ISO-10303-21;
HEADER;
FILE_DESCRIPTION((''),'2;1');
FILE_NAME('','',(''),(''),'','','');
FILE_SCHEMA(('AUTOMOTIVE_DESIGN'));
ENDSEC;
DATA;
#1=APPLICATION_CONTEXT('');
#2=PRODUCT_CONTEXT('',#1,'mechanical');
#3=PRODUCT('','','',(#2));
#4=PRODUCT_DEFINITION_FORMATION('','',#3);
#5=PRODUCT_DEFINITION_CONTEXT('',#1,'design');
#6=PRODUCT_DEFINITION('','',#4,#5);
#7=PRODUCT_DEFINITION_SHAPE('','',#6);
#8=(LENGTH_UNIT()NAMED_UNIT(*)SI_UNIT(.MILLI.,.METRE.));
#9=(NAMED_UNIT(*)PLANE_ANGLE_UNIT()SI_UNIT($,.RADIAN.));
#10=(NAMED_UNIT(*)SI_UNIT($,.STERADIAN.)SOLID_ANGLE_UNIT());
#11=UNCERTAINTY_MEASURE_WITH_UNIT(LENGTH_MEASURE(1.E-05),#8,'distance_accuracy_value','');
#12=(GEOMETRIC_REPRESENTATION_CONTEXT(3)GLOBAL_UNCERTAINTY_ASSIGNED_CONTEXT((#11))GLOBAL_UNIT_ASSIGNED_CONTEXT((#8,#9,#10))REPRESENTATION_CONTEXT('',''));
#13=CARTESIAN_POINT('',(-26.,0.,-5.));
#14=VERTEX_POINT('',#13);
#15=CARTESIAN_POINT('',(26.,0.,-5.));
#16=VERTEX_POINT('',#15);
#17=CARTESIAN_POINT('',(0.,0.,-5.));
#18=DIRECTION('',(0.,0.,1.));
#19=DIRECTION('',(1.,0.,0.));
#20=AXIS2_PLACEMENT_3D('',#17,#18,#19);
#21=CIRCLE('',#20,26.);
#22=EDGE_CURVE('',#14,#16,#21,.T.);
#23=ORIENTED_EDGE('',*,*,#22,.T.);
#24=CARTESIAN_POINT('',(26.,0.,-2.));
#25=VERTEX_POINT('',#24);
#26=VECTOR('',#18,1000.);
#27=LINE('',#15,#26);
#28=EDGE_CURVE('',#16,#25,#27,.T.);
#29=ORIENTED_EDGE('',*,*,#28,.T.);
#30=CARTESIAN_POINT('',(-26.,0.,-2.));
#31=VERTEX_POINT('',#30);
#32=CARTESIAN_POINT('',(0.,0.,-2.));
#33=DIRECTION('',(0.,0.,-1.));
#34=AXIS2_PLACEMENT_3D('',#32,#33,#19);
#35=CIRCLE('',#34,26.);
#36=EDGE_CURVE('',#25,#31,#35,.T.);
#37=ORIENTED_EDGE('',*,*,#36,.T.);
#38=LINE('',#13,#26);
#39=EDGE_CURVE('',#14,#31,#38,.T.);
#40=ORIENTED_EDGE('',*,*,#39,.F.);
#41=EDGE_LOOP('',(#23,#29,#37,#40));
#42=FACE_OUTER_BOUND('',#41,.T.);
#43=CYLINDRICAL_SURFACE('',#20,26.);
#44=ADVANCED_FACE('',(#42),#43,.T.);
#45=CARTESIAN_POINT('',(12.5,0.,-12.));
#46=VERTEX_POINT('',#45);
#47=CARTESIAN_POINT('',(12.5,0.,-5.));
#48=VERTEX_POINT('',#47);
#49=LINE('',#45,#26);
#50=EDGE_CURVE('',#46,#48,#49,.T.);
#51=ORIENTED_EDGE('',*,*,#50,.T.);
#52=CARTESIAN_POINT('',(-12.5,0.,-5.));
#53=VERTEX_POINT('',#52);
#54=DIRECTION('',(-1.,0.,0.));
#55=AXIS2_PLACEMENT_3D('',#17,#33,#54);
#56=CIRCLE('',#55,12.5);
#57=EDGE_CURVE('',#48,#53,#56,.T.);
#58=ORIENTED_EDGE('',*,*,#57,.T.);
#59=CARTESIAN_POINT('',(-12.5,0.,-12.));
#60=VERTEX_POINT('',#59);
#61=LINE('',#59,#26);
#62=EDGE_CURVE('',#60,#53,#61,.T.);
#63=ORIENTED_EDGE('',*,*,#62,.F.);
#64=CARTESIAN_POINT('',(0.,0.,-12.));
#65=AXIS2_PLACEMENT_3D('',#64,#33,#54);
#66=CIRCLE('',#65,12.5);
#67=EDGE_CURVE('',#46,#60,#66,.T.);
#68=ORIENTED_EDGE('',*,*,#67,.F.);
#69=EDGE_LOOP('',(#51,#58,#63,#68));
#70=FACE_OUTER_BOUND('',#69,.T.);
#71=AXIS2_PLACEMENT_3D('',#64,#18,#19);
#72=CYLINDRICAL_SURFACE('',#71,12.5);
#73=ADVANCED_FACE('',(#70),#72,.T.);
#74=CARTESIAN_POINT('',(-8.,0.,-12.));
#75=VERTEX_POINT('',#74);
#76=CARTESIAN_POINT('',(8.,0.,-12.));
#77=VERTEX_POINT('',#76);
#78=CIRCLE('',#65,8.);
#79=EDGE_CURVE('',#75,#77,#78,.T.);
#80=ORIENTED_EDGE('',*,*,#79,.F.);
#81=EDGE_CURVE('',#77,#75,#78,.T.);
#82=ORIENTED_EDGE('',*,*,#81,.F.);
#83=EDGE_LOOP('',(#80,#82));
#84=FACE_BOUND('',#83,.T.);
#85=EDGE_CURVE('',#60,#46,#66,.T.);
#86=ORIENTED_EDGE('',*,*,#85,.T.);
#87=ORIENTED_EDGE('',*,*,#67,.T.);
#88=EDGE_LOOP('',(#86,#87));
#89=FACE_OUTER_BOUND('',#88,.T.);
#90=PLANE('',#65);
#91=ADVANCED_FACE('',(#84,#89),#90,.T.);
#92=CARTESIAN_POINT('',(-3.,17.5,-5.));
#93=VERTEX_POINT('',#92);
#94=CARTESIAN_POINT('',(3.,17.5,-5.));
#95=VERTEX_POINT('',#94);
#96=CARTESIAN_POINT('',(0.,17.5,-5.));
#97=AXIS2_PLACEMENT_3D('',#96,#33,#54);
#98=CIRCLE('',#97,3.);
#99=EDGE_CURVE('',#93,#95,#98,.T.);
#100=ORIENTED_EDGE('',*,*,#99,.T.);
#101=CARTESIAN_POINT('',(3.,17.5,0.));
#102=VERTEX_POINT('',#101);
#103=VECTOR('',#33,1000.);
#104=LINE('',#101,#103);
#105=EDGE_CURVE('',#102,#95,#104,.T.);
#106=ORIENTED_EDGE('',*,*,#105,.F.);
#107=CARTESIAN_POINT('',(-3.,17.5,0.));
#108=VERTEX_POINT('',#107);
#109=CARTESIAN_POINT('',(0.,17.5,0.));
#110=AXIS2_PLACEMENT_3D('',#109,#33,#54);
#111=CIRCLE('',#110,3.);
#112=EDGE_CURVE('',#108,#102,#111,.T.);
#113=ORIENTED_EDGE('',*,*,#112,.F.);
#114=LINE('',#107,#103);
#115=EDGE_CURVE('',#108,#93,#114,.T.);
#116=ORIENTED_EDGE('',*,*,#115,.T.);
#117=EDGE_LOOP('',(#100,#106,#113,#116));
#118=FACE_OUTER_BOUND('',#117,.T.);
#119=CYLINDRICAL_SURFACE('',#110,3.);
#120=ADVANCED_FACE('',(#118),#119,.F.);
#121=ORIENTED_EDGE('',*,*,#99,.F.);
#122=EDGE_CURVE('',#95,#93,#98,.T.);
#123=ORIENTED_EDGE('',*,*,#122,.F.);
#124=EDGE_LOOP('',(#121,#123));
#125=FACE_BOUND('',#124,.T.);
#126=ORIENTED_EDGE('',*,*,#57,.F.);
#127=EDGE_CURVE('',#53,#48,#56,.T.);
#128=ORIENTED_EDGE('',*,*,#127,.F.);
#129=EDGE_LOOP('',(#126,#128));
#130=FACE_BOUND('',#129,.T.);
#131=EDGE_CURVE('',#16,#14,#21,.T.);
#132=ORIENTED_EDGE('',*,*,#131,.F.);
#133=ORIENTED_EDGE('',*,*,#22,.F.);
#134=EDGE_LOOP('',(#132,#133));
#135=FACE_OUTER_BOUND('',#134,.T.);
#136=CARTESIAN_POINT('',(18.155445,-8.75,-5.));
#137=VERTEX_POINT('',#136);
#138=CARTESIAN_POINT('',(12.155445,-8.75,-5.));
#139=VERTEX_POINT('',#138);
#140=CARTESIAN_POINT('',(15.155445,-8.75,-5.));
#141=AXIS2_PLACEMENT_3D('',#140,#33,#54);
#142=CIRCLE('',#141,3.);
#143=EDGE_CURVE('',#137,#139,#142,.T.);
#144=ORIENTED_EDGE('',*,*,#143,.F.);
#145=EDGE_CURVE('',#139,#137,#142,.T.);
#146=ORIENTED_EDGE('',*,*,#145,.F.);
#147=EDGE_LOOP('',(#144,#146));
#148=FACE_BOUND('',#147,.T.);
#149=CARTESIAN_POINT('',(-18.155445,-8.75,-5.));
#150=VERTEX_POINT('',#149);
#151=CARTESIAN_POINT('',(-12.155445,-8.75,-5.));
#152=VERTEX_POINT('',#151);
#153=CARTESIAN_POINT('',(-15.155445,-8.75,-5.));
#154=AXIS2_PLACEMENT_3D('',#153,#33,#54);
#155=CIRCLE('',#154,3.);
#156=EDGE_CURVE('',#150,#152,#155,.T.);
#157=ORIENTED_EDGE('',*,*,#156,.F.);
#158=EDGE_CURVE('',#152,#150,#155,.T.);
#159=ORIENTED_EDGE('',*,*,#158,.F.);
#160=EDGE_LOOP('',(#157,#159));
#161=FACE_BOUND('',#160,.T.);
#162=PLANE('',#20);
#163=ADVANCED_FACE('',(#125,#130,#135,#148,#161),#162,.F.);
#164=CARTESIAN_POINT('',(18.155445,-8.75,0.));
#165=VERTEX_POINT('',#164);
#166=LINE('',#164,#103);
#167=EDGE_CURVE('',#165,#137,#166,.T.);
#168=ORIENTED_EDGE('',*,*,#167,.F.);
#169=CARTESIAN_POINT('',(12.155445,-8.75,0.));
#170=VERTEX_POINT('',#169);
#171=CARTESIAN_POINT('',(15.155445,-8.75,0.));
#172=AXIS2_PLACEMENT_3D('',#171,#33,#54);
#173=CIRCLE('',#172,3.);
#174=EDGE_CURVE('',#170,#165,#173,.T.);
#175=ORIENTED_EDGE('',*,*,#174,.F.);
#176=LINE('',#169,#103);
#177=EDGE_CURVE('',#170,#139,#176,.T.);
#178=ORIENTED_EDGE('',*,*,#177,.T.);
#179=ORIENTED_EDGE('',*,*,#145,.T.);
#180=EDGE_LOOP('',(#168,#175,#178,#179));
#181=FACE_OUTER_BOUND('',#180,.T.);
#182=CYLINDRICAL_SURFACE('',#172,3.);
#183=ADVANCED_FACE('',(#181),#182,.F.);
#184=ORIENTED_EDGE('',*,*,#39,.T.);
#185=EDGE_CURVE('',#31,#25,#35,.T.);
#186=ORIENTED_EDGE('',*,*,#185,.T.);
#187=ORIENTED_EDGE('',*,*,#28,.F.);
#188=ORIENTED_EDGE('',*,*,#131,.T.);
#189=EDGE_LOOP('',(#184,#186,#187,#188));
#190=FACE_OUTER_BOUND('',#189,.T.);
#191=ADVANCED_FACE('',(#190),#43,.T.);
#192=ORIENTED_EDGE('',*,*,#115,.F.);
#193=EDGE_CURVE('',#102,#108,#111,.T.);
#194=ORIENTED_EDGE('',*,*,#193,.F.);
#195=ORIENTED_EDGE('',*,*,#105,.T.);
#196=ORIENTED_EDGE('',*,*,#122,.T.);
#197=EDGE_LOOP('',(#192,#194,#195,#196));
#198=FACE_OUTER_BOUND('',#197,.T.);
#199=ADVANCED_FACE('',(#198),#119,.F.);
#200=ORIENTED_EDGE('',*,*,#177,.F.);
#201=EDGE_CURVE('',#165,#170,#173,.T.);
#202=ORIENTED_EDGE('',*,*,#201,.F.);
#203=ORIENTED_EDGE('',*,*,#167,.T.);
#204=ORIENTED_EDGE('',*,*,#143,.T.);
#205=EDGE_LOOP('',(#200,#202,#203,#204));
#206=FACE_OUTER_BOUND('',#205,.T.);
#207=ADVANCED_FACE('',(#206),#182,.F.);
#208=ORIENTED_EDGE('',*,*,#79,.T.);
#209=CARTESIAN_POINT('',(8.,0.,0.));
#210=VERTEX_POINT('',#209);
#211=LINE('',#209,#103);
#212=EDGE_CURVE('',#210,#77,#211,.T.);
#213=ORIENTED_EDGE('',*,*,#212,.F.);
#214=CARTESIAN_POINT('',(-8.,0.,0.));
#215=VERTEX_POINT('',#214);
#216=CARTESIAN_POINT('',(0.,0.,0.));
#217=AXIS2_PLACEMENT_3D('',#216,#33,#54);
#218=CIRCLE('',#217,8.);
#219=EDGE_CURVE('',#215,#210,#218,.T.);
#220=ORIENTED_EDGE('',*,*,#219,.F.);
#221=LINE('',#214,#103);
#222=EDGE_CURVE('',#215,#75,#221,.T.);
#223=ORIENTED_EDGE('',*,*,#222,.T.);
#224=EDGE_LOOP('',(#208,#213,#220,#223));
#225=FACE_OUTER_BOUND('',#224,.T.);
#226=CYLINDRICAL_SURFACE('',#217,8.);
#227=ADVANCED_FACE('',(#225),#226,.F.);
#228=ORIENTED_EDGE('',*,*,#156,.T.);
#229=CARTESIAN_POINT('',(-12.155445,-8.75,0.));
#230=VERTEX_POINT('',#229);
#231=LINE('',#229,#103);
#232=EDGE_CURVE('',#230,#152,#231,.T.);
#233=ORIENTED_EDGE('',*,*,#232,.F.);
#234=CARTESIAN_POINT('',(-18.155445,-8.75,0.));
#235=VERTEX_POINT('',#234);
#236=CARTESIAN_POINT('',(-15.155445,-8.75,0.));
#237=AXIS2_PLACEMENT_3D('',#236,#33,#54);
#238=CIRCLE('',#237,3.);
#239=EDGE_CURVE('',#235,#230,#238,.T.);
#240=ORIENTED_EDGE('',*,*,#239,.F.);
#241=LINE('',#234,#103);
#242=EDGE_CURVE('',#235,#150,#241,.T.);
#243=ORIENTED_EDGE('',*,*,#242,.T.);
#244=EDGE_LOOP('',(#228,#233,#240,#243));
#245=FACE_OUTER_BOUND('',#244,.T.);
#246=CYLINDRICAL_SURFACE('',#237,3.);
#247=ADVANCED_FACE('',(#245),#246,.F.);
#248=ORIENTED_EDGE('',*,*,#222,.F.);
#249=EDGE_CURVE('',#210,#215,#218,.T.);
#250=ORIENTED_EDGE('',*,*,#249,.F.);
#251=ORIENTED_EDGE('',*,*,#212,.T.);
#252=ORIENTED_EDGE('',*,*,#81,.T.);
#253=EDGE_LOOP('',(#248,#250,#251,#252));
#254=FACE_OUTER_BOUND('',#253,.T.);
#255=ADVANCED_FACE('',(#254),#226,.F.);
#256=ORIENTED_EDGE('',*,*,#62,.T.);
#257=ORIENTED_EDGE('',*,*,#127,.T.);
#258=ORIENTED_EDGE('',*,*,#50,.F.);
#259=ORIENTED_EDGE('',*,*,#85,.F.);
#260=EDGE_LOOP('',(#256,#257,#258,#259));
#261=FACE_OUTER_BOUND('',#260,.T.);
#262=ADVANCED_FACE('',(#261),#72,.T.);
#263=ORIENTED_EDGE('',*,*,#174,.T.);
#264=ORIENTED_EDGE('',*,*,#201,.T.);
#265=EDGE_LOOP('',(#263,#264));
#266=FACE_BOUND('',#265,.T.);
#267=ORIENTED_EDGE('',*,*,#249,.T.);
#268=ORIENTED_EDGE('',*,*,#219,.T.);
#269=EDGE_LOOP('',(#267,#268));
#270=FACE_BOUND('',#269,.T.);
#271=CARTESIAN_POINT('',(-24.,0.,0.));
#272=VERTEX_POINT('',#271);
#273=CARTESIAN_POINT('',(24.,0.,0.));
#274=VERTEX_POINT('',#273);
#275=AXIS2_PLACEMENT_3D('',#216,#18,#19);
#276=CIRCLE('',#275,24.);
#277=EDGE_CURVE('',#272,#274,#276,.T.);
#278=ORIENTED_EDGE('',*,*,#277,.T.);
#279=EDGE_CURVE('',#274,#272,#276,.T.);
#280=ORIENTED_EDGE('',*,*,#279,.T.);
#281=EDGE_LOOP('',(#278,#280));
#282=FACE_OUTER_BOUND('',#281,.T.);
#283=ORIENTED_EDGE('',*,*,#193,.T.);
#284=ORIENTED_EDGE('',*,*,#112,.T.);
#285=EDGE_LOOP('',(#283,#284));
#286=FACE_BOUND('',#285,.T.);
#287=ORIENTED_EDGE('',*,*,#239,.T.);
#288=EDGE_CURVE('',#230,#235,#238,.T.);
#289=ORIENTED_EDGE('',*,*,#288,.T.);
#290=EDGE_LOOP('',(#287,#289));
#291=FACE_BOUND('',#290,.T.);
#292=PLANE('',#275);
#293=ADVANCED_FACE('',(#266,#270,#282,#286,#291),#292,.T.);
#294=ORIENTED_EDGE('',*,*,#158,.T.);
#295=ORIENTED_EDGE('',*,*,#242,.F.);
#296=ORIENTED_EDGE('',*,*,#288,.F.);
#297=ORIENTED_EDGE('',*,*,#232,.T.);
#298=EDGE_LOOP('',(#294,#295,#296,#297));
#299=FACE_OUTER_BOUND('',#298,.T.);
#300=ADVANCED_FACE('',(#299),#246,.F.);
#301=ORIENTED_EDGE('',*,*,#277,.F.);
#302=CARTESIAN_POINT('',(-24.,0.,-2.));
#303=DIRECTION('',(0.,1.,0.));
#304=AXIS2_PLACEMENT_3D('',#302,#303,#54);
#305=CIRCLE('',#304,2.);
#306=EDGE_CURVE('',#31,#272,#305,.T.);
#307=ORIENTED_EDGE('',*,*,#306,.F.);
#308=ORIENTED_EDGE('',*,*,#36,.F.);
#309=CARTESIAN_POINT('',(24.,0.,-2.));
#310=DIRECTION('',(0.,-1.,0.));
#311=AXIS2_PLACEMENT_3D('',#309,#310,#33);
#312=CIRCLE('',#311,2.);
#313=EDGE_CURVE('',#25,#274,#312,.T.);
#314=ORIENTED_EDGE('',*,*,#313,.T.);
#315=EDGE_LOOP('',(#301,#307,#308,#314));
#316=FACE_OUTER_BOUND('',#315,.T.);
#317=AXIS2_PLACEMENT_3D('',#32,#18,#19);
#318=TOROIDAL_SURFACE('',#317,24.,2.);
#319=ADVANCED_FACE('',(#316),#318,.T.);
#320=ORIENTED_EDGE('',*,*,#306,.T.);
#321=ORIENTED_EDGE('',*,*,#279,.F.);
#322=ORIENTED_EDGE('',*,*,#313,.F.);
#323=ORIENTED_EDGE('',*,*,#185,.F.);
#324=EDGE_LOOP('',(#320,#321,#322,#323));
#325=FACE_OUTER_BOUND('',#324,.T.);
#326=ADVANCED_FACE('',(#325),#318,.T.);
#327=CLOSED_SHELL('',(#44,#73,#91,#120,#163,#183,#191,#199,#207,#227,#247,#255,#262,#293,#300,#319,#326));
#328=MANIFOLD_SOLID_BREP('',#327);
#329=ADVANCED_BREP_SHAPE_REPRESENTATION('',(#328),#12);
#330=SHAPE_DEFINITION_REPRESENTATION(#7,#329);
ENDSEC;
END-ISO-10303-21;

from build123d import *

# Parameters (mm, degrees)
FLANGE_PROFILE_R                 = 26
FLANGE_52_DEPTH                  = 5
HUB_PROFILE_R                    = 12.5
HUB_25_DEPTH                     = 7
BORE_16_DEPTH                    = 39.678159212
BORE_16_DEPTH_BACK               = 39.678159212
BORE_PROFILE_R                   = 8
BOLT_HOLES_3X_6_PCD35_DEPTH      = 38.429934544
BOLT_HOLES_3X_6_PCD35_DEPTH_BACK = 38.429934544
BOLT_HOLE_PROFILE_R              = 3
FLANGE_EDGE_FILLET_R2_R          = 2


with BuildPart() as part:
    # Flange Profile → Flange Ø52 (new body)
    with BuildSketch(Plane.XY):
        Circle(FLANGE_PROFILE_R)
    extrude(amount=-FLANGE_52_DEPTH)

    # Hub Profile → Hub Ø25 (add)
    with BuildSketch(Plane(origin=(0, 0, -5), x_dir=(-1, 0, 0), z_dir=(0, 0, -1))):
        Circle(HUB_PROFILE_R)
    extrude(amount=HUB_25_DEPTH)

    # Bore Profile → Bore Ø16 (cut, two sides: drawn at the far end of the back side and taken through both)
    with BuildSketch(Plane(origin=(0, 0, -12), x_dir=(-1, 0, 0), z_dir=(0, 0, -1)).offset(-BORE_16_DEPTH_BACK)):
        Circle(BORE_PROFILE_R)
    extrude(amount=BORE_16_DEPTH + BORE_16_DEPTH_BACK, mode=Mode.SUBTRACT)

    # Bolt Hole Profile → Bolt Holes 3xØ6 PCD35 (cut, two sides: drawn at the far end of the back side and taken through both)
    with BuildSketch(Plane(origin=(0, 0, -5), x_dir=(-1, 0, 0), z_dir=(0, 0, -1)).offset(-BOLT_HOLES_3X_6_PCD35_DEPTH_BACK)):
        with Locations((0, 17.5)):
            Circle(BOLT_HOLE_PROFILE_R)
        with Locations((15.155444566, -8.75)):
            Circle(BOLT_HOLE_PROFILE_R)
        with Locations((-15.155444566, -8.75)):
            Circle(BOLT_HOLE_PROFILE_R)
    extrude(amount=BOLT_HOLES_3X_6_PCD35_DEPTH + BOLT_HOLES_3X_6_PCD35_DEPTH_BACK, mode=Mode.SUBTRACT)

    # Flange Edge Fillet R2
    flange_edge_fillet_r2_edges = [part.edges().sort_by_distance(p)[0] for p in [
        (-26, 0, 0),
    ]]
    fillet(flange_edge_fillet_r2_edges, radius=FLANGE_EDGE_FILLET_R2_R)


solid = part.part
